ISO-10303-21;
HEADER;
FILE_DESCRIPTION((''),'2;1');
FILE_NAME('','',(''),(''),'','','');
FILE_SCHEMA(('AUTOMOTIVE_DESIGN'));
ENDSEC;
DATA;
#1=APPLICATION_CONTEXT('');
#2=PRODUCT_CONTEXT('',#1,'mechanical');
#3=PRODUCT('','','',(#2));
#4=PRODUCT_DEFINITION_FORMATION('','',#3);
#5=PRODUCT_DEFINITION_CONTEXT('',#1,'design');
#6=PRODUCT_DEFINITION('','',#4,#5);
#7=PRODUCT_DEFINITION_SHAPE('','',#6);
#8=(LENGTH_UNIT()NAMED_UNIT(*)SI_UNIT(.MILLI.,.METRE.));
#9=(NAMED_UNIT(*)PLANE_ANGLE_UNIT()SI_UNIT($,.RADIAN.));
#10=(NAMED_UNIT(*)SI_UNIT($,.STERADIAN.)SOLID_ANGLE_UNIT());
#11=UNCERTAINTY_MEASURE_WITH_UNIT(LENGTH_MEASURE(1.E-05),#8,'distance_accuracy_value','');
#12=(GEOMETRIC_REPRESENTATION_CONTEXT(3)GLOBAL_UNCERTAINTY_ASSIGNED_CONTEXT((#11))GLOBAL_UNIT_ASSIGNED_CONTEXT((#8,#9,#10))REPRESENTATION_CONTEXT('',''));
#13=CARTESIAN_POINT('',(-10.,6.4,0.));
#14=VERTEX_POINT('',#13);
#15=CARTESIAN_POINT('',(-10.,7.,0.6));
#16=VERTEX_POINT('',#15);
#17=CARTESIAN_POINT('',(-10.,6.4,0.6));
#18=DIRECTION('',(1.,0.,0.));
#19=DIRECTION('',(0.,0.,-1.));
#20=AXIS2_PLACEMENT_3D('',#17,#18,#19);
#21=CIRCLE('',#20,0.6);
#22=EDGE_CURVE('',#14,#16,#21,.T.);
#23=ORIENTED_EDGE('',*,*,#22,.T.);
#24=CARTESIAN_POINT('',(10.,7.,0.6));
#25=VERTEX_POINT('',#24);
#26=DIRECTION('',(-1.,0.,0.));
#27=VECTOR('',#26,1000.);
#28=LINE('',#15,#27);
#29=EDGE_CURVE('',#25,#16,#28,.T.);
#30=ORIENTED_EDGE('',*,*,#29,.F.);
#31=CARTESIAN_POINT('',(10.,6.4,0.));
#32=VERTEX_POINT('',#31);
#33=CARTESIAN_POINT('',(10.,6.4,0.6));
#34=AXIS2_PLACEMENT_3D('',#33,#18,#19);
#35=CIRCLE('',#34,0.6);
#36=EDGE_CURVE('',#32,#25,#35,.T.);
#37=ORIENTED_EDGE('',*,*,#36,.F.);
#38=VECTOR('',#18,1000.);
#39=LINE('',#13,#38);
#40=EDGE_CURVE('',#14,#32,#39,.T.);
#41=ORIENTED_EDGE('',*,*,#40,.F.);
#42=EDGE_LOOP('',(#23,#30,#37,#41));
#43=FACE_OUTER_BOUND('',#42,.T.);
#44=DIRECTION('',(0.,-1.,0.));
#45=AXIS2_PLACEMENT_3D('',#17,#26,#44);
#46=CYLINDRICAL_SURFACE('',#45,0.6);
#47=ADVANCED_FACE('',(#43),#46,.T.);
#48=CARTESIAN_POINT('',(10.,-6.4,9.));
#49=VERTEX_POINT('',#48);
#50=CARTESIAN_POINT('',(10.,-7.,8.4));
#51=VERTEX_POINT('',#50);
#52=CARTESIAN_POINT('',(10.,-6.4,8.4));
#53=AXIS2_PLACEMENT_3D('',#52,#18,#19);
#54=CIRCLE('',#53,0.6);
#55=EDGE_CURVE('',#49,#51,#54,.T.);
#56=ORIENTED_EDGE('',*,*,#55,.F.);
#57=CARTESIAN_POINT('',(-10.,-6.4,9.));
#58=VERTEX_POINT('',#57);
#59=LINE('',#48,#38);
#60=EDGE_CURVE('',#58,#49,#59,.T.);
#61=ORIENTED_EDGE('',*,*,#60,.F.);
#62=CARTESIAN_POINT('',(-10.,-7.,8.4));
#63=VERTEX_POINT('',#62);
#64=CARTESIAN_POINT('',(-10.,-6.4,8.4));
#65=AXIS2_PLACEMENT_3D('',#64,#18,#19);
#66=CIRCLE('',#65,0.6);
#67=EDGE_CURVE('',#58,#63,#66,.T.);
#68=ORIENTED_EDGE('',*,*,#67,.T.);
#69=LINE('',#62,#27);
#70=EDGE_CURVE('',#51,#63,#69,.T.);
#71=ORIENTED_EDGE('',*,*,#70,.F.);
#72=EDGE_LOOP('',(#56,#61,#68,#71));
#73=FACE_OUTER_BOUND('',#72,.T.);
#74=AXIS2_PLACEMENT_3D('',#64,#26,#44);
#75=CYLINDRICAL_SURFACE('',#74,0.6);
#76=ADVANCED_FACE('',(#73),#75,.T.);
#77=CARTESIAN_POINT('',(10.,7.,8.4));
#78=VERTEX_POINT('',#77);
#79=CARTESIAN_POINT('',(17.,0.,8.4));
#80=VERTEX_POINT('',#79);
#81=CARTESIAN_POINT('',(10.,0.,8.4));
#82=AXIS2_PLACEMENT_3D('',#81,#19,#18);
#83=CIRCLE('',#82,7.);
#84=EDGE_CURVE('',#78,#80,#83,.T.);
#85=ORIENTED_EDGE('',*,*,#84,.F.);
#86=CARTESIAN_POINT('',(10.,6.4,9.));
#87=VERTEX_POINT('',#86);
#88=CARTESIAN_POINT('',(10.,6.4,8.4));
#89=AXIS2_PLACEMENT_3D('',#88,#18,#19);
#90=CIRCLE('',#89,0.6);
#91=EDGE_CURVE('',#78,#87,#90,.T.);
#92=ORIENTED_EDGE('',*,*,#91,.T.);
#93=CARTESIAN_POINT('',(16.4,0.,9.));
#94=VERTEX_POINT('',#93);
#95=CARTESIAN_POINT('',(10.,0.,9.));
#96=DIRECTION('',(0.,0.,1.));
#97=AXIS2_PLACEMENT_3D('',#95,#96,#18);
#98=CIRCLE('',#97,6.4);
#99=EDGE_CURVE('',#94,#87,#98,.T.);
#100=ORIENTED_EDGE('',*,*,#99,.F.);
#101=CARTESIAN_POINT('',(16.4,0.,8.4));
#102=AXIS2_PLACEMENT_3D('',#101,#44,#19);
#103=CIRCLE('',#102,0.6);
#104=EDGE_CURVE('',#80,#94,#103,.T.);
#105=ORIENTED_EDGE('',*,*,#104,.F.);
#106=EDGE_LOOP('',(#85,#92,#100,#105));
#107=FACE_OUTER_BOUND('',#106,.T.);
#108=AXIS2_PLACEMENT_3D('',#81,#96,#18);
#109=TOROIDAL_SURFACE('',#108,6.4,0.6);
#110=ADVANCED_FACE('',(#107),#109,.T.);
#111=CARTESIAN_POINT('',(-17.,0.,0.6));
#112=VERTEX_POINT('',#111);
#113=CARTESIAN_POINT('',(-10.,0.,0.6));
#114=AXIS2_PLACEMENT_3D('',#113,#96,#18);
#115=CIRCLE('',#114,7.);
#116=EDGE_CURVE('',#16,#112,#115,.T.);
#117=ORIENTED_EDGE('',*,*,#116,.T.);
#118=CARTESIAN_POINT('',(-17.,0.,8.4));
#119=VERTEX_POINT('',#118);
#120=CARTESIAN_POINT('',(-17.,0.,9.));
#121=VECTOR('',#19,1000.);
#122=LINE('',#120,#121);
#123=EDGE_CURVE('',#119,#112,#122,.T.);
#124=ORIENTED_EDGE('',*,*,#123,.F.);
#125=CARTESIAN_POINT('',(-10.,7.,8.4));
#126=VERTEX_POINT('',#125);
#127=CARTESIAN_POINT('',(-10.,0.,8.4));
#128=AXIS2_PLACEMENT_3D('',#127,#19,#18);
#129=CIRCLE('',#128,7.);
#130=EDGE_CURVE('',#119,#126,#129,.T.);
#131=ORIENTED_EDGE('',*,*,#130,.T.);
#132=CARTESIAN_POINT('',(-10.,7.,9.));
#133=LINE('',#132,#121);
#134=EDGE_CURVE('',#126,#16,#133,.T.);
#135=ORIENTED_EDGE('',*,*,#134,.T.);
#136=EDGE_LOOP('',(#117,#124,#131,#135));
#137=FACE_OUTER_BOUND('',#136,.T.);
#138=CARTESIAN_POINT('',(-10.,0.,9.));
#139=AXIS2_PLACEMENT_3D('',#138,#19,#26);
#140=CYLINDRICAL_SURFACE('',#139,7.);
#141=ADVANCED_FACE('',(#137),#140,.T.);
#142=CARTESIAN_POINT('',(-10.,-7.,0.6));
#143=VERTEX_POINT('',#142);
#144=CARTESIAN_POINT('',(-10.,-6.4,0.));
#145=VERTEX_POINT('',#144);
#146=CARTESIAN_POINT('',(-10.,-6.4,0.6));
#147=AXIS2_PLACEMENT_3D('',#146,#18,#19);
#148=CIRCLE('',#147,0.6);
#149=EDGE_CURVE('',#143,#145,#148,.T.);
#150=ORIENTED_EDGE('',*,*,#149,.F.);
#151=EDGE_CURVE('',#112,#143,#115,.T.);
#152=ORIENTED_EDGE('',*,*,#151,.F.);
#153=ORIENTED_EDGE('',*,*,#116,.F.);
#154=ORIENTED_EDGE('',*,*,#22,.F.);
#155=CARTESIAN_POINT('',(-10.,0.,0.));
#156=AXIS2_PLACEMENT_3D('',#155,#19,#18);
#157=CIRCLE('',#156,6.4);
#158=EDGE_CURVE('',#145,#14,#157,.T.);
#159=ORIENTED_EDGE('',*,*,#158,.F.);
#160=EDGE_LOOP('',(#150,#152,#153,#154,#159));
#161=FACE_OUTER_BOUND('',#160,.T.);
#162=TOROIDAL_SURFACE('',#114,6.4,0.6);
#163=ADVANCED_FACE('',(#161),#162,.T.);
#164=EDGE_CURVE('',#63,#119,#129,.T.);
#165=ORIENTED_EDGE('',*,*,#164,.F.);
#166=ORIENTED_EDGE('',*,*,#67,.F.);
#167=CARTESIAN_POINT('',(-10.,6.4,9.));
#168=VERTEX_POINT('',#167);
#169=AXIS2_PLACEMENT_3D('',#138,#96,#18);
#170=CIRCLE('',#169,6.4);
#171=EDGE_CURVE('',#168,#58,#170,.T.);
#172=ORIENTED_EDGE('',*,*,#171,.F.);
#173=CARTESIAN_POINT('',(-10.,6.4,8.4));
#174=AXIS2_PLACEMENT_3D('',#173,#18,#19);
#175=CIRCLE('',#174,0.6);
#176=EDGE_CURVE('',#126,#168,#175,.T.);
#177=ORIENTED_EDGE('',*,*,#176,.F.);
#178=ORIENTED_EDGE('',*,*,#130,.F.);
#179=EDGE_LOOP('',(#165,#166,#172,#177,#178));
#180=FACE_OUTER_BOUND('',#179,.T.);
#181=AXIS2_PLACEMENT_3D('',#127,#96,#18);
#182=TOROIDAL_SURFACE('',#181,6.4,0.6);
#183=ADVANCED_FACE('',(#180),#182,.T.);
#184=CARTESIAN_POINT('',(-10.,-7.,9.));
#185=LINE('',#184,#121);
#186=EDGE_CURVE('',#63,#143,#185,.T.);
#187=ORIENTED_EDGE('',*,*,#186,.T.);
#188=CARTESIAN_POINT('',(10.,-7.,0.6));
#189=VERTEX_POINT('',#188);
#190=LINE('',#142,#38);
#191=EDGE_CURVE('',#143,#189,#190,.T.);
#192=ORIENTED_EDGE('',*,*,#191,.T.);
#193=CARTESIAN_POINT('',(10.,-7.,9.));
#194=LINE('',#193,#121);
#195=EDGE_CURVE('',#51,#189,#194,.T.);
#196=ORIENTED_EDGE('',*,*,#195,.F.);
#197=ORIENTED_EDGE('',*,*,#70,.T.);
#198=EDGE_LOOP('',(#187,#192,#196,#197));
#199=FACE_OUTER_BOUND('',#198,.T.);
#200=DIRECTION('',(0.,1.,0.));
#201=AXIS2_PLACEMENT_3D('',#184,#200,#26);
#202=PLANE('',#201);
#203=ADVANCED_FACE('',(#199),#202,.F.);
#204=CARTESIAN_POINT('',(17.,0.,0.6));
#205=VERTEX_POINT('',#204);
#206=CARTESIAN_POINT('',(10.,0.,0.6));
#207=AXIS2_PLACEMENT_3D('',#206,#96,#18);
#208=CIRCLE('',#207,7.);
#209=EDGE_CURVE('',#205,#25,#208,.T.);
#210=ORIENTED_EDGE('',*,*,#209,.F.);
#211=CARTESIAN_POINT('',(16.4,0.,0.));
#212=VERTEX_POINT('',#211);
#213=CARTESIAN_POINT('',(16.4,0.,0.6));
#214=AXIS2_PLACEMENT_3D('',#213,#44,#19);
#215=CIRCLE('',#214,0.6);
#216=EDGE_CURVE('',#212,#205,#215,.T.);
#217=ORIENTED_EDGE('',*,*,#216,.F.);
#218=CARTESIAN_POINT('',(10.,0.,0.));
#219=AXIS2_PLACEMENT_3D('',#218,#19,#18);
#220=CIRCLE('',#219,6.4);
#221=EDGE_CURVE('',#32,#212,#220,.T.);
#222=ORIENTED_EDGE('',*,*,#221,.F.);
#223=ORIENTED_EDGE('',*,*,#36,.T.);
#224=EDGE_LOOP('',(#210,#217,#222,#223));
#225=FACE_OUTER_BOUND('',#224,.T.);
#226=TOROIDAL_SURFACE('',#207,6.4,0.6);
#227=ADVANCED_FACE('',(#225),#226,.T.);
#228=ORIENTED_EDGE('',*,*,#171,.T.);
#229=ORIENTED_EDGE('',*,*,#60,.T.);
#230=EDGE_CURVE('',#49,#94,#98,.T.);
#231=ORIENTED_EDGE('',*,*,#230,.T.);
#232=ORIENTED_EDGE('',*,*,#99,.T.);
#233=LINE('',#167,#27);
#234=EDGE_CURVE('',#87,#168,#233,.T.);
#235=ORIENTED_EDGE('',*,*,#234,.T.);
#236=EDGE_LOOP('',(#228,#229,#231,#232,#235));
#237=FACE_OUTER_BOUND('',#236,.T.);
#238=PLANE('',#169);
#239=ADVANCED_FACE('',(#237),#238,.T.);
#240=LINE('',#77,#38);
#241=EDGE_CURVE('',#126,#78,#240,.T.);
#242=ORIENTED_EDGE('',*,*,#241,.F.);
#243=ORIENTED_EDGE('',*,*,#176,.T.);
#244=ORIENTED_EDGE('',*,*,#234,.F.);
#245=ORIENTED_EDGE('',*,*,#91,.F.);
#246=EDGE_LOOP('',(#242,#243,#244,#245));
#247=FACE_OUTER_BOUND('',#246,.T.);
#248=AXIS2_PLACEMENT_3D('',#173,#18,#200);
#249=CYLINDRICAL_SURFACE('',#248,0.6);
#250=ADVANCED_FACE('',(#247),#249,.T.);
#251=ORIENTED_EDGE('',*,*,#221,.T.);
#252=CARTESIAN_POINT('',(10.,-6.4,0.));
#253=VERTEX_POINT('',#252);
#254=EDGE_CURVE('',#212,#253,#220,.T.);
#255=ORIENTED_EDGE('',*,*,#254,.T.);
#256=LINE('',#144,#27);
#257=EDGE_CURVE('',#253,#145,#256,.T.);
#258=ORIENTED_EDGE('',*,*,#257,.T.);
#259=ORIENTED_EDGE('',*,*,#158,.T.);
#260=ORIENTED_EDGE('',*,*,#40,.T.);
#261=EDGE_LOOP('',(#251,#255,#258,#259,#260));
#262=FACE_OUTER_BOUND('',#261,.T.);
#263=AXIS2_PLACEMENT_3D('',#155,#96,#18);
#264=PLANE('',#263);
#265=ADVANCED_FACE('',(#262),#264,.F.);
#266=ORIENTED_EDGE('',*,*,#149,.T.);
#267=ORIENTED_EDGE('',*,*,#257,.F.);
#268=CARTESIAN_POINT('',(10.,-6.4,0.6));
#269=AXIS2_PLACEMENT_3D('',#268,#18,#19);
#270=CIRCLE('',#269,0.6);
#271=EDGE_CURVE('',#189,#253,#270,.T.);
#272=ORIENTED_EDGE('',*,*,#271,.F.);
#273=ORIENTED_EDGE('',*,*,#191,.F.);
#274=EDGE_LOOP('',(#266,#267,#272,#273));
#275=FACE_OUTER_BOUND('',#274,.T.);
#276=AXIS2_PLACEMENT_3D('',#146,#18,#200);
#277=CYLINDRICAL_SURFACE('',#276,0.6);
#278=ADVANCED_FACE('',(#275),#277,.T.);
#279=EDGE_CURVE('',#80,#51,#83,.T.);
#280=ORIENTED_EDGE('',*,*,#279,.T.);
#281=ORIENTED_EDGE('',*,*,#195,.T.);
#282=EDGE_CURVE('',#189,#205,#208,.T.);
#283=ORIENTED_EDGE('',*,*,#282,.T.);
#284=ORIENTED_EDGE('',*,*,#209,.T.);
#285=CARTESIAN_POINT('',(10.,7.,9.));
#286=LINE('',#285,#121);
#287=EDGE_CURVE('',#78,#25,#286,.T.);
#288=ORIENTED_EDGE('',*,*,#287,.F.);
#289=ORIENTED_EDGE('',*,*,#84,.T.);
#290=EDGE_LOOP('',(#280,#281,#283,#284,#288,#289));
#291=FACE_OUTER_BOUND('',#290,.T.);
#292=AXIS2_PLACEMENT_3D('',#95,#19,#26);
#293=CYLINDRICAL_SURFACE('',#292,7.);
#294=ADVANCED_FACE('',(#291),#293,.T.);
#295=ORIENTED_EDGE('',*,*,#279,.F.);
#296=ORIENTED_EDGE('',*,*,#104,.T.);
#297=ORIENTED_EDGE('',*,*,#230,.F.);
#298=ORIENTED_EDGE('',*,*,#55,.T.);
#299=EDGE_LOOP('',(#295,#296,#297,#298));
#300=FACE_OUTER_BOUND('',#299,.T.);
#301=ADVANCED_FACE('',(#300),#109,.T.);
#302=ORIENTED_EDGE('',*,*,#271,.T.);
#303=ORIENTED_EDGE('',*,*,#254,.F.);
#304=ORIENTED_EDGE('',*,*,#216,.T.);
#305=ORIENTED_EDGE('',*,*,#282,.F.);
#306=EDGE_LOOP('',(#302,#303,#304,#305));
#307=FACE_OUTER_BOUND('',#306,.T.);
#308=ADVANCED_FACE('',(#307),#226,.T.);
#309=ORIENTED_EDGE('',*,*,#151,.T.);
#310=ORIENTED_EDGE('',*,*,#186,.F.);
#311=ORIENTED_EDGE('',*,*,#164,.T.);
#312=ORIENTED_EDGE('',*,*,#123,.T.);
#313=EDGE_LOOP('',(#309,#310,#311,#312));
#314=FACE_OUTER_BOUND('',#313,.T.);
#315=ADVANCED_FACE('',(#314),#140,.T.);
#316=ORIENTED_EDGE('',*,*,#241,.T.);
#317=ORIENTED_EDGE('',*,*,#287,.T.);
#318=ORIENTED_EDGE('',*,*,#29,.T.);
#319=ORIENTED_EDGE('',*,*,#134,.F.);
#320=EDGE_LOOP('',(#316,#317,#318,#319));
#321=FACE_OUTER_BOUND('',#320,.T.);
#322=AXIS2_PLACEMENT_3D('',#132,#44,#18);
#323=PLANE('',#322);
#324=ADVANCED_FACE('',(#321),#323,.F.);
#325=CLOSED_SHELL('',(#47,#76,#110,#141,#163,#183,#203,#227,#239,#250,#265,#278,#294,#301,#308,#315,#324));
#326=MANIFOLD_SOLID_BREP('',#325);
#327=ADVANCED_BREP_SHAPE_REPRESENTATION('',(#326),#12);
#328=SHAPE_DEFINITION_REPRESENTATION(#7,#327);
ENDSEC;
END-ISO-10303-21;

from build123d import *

# Parameters (mm, degrees)
EXTRUDE_524_DEPTH = 9
FILLET_1_R        = 0.6


with BuildPart() as part:
    # 草图1 → Extrude 524 (new body)
    with BuildSketch(Plane.XY):
        with BuildLine():
            Line((-10, 7), (10, 7))
            ThreePointArc((10, 7), (17, 0), (10, -7))
            Line((10, -7), (-10, -7))
            ThreePointArc((-10, -7), (-17, 0), (-10, 7))
        make_face()
    extrude(amount=EXTRUDE_524_DEPTH)

    # 圆角1
    fillet_1_edges = [part.edges().sort_by_distance(p)[0] for p in [
        (17, 0, 9),
        (0, 7, 9),
        (-17, 0, 9),
        (0, 7, 0),
        (17, 0, 0),
        (0, -7, 0),
        (-17, 0, 0),
        (0, -7, 9),
    ]]
    fillet(fillet_1_edges, radius=FILLET_1_R)


solid = part.part
